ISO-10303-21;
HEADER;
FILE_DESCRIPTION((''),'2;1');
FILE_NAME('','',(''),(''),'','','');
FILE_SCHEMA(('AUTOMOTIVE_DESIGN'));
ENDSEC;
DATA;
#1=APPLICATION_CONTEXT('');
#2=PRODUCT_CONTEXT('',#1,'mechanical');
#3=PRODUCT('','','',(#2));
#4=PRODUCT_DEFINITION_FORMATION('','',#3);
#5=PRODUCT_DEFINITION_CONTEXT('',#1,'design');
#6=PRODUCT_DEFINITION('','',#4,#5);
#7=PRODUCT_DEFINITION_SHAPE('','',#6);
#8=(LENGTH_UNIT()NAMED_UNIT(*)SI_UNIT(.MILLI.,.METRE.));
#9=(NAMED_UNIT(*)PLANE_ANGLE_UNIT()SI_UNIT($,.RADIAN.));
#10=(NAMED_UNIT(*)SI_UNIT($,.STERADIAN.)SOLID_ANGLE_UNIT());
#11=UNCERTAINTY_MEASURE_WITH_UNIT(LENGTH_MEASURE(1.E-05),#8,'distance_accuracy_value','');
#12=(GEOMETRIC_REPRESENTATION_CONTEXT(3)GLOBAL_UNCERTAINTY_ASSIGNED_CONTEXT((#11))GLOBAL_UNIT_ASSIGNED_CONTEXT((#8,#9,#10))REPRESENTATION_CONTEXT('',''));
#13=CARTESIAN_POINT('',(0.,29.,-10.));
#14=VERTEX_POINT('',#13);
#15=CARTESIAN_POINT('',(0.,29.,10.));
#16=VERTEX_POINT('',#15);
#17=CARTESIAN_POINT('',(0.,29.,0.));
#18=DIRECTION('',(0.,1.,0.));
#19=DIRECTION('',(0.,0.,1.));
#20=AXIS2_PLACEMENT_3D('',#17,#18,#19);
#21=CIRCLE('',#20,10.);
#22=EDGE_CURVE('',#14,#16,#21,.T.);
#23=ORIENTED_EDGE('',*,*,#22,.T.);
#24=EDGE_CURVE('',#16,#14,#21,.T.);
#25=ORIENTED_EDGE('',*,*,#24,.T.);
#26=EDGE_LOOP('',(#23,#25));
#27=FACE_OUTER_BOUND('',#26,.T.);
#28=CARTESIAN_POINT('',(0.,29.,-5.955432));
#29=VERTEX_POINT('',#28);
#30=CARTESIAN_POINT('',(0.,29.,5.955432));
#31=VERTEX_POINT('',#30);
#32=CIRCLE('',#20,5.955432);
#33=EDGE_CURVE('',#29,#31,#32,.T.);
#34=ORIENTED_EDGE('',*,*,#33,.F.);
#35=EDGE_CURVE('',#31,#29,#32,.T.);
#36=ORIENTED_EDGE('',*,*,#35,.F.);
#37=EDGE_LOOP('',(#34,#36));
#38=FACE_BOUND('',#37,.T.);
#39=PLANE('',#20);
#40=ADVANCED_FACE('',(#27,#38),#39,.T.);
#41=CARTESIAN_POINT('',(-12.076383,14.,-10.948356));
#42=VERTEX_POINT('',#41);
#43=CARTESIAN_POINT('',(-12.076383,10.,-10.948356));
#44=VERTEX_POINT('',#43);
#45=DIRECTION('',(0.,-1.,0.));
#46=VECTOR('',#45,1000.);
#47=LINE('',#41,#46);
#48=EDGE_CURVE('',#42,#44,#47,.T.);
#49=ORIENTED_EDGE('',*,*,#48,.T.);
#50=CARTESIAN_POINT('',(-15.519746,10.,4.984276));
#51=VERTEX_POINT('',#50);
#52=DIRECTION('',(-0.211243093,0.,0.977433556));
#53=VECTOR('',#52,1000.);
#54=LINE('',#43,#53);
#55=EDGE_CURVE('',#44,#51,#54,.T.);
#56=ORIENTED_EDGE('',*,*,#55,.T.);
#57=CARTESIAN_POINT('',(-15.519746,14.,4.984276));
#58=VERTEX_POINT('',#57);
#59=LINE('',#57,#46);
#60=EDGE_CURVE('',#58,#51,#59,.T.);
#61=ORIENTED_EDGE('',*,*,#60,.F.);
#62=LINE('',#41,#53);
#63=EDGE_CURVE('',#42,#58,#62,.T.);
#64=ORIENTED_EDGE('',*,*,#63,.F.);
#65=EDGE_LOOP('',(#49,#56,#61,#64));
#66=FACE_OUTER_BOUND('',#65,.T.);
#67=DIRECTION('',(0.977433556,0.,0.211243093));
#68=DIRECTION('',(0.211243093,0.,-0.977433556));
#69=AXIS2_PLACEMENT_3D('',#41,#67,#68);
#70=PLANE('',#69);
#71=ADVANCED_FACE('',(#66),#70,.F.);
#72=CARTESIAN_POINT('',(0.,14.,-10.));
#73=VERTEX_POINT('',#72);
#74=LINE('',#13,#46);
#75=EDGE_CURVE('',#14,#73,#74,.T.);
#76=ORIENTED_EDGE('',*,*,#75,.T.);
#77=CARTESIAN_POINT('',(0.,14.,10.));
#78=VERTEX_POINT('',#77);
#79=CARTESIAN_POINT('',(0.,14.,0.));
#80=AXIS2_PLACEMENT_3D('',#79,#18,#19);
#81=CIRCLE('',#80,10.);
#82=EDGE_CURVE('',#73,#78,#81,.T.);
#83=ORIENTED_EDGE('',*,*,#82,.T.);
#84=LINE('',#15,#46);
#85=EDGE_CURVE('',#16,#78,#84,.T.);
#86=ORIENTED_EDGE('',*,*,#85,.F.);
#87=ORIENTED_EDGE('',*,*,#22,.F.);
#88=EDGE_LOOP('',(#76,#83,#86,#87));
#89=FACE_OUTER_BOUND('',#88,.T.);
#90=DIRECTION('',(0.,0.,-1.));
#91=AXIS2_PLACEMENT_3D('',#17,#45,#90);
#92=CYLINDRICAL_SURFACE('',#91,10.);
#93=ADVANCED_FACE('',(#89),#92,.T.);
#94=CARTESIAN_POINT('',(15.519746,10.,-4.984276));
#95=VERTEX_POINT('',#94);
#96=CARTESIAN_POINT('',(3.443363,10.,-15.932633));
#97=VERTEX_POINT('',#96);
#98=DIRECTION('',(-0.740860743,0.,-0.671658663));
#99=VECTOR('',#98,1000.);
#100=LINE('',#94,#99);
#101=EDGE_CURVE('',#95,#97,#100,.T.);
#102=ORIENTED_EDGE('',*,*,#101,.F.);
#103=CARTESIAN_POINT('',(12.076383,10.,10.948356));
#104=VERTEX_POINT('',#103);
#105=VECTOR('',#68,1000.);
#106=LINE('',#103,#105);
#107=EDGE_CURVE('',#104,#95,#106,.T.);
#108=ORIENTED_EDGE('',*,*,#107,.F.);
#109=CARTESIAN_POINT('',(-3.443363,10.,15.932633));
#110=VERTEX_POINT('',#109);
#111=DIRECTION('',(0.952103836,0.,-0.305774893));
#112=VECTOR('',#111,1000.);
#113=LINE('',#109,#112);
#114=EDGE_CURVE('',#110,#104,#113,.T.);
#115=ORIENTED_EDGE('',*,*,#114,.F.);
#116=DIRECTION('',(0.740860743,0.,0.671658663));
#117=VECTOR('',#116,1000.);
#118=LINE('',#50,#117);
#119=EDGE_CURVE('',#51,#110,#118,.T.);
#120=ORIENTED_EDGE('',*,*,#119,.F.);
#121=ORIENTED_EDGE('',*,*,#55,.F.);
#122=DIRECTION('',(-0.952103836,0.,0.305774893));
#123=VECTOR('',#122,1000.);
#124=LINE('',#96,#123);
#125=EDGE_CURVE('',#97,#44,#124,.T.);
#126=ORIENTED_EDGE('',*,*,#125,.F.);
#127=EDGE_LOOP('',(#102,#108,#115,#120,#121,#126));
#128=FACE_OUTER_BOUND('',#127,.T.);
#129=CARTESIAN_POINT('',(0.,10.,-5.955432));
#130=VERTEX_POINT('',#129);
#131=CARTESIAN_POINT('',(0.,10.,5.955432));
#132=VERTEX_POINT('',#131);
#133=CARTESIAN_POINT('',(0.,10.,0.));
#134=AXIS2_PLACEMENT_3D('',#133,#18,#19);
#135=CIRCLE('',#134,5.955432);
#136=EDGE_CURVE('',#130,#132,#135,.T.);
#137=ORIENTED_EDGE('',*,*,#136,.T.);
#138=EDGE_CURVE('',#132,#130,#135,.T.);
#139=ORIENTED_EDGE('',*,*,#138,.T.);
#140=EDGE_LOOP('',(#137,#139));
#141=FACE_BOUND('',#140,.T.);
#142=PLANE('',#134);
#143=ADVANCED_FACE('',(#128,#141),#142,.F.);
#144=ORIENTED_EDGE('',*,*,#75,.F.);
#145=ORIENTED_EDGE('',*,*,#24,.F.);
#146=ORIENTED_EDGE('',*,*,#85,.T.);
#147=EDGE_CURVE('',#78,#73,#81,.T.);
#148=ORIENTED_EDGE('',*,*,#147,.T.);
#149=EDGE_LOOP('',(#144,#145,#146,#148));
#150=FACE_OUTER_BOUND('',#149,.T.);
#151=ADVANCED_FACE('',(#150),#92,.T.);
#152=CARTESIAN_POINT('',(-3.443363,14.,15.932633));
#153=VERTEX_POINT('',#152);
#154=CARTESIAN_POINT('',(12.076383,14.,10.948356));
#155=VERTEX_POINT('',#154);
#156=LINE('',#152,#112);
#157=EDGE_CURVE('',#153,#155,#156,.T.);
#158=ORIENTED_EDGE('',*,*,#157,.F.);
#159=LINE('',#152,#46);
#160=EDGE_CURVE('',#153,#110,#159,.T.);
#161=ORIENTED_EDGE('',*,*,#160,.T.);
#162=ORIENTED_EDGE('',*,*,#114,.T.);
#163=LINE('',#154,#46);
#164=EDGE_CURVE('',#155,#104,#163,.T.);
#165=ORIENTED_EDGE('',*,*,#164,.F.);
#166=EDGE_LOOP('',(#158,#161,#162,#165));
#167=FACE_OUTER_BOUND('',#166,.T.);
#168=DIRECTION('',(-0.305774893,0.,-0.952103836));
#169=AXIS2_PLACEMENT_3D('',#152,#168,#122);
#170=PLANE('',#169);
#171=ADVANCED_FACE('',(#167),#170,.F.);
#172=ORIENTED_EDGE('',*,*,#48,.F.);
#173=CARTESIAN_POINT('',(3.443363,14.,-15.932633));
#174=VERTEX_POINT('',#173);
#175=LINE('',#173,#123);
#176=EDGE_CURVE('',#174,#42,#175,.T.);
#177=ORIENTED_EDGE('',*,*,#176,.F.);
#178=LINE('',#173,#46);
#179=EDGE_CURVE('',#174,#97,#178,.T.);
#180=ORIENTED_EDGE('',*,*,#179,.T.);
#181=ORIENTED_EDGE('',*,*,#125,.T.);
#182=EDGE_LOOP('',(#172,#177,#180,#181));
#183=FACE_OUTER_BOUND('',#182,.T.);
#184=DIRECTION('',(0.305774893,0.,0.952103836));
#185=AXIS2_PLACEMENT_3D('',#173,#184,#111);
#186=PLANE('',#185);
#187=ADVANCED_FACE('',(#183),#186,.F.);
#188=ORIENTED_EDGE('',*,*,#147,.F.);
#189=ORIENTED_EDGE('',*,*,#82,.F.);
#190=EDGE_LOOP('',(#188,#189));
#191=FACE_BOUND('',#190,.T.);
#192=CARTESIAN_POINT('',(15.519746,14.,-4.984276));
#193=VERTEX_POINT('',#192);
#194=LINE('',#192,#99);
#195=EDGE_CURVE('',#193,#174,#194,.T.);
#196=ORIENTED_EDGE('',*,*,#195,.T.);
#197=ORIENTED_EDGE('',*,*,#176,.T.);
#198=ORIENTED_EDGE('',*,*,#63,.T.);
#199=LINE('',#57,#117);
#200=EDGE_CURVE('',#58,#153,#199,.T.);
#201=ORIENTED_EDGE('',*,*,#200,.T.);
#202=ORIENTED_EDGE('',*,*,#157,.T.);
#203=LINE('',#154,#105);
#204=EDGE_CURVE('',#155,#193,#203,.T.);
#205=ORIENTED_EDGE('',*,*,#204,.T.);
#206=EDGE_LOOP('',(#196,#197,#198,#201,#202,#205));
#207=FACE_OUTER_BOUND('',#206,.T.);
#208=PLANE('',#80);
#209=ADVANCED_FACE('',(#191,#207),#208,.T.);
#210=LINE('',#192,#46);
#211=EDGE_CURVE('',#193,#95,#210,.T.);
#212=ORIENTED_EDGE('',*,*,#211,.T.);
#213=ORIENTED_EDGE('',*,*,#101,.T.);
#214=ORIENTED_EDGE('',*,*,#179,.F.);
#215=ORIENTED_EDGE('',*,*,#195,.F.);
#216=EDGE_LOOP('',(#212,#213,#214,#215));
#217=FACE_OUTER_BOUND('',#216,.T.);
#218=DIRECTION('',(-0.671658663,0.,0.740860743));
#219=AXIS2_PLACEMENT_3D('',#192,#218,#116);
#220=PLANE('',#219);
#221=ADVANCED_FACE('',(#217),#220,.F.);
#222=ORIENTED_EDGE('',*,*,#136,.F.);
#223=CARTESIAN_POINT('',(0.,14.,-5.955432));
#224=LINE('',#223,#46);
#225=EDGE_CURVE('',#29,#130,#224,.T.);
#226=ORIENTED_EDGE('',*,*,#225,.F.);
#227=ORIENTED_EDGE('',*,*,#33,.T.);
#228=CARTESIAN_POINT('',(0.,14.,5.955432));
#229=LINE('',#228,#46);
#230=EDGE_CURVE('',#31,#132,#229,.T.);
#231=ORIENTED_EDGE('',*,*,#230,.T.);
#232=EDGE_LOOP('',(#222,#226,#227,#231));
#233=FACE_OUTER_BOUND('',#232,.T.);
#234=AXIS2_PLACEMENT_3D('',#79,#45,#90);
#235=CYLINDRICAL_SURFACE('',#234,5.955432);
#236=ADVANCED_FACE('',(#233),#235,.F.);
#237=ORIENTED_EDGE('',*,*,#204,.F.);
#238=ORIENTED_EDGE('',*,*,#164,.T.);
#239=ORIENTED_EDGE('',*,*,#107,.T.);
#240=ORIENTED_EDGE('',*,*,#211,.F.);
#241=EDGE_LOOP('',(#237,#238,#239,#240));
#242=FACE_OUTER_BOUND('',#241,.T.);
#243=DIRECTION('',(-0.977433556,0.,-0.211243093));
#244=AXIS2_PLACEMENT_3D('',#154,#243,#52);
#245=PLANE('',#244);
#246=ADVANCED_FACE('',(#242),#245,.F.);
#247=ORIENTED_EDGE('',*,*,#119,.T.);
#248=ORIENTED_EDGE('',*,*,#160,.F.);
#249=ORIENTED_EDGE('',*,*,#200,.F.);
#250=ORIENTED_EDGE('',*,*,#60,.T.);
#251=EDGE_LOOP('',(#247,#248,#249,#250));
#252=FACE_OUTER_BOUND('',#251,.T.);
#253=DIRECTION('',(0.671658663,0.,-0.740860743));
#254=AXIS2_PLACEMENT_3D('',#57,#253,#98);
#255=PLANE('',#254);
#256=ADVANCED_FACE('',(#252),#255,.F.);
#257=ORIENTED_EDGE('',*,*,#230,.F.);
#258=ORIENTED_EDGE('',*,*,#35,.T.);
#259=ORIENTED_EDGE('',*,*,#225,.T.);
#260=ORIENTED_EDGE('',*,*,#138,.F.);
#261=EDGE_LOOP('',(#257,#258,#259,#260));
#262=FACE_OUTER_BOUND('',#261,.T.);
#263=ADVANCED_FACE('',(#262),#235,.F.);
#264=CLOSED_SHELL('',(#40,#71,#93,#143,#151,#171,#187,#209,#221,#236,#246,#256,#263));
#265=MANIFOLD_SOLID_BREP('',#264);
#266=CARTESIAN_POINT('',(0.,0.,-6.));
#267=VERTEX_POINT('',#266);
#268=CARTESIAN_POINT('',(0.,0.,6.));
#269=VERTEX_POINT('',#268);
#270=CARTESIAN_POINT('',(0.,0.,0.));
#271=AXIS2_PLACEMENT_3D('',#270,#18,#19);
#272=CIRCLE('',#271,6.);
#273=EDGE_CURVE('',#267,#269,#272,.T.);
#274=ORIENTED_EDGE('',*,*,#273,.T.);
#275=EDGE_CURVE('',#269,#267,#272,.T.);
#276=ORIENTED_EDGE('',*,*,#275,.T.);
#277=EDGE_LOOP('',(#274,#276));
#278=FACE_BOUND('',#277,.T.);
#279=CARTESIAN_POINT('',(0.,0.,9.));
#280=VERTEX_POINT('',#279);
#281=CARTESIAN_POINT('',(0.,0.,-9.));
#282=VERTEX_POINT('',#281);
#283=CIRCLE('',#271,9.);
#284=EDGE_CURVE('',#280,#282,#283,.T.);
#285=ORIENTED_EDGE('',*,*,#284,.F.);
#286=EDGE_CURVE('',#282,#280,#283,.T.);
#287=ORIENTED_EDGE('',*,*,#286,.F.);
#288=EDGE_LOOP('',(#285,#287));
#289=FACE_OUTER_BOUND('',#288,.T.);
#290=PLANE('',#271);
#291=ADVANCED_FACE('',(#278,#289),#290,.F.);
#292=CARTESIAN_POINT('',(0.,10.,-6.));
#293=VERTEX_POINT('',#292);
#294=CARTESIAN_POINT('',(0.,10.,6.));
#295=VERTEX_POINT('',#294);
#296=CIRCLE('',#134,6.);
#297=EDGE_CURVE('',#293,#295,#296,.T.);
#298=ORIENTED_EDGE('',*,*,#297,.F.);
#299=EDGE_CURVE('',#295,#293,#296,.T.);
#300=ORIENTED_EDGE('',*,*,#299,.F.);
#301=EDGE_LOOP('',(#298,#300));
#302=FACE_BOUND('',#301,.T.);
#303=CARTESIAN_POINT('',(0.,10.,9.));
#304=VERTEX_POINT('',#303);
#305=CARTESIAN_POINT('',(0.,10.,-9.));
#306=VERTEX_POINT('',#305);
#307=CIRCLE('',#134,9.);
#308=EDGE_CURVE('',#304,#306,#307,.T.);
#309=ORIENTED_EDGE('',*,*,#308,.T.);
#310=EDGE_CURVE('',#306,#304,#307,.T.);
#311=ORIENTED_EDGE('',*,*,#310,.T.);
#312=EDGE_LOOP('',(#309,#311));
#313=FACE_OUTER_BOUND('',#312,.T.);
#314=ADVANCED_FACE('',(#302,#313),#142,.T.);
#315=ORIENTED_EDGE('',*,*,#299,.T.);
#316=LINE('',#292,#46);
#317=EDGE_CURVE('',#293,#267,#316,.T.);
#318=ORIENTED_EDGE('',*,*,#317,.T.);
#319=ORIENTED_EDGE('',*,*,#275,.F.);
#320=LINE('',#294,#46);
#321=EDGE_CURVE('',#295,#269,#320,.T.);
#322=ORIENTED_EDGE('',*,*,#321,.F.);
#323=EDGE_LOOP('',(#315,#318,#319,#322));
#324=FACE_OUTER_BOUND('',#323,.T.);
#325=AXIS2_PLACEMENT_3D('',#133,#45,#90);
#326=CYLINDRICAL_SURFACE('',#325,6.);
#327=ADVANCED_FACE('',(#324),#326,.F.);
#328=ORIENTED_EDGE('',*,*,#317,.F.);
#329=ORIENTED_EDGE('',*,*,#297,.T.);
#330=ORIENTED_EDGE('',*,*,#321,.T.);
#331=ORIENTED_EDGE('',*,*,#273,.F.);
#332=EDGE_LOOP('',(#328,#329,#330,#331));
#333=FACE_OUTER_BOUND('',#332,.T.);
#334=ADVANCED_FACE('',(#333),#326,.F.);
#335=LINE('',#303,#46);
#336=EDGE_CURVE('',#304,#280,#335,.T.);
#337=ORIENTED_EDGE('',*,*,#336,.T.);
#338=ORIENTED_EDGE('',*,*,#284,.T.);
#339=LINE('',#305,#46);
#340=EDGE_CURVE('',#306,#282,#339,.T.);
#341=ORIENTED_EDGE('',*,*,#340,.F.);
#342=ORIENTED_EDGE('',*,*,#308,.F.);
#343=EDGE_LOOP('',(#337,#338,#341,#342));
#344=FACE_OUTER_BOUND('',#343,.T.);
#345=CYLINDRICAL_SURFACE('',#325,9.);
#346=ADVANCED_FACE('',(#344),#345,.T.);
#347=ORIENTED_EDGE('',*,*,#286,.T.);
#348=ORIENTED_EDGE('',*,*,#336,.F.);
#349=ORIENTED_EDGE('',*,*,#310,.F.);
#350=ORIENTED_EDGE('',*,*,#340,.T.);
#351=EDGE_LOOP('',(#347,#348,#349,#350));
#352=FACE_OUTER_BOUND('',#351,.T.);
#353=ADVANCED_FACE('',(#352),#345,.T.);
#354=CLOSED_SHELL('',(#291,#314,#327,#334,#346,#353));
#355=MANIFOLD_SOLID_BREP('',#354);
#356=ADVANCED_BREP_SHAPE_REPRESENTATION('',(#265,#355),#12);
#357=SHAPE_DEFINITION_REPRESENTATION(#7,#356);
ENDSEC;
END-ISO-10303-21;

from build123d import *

# Parameters (mm, degrees)
SKETCH1_R           = 9
SKETCH1_R_2         = 6
BOSS_EXTRUDE1_DEPTH = 10
SKETCH2_R           = 5.955432099
BOSS_EXTRUDE2_DEPTH = 4
SKETCH3_R           = 10
SKETCH3_R_2         = 5.955432099
BOSS_EXTRUDE3_DEPTH = 15


with BuildPart() as part:
    # Sketch1 → Boss-Extrude1 (new body)
    with BuildSketch(Plane(origin=(0, 0, 0), x_dir=(1, 0, 0), z_dir=(0, 1, 0))):
        with Locations(Location((0, 0, 0), (0, 0, 270))):
            Circle(SKETCH1_R)
        with Locations(Location((0, 0, 0), (0, 0, 270))):
            Circle(SKETCH1_R_2, mode=Mode.SUBTRACT)
    extrude(amount=BOSS_EXTRUDE1_DEPTH)


with BuildPart() as body_2:
    # Sketch2 → Boss-Extrude2 (new body)
    with BuildSketch(Plane(origin=(0, 10, 0), x_dir=(1, 0, 0), z_dir=(0, 1, 0))):
        Polygon((-12.076383081, 10.948356194), (-15.519746134, -4.984276437), (-3.443363053, -15.93263263), (12.076383081, -10.948356194), (15.519746134, 4.984276437), (3.443363053, 15.93263263), align=None)
        with Locations(Location((0, 0, 0), (0, 0, 270))):
            Circle(SKETCH2_R, mode=Mode.SUBTRACT)
    extrude(amount=BOSS_EXTRUDE2_DEPTH)

    # Sketch3 → Boss-Extrude3 (add)
    with BuildSketch(Plane(origin=(0, 14, 0), x_dir=(1, 0, 0), z_dir=(0, 1, 0))):
        with Locations(Location((0, 0, 0), (0, 0, 270))):
            Circle(SKETCH3_R)
        with Locations(Location((0, 0, 0), (0, 0, 270))):
            Circle(SKETCH3_R_2, mode=Mode.SUBTRACT)
    extrude(amount=BOSS_EXTRUDE3_DEPTH)


solid = Compound([part.part, body_2.part])
